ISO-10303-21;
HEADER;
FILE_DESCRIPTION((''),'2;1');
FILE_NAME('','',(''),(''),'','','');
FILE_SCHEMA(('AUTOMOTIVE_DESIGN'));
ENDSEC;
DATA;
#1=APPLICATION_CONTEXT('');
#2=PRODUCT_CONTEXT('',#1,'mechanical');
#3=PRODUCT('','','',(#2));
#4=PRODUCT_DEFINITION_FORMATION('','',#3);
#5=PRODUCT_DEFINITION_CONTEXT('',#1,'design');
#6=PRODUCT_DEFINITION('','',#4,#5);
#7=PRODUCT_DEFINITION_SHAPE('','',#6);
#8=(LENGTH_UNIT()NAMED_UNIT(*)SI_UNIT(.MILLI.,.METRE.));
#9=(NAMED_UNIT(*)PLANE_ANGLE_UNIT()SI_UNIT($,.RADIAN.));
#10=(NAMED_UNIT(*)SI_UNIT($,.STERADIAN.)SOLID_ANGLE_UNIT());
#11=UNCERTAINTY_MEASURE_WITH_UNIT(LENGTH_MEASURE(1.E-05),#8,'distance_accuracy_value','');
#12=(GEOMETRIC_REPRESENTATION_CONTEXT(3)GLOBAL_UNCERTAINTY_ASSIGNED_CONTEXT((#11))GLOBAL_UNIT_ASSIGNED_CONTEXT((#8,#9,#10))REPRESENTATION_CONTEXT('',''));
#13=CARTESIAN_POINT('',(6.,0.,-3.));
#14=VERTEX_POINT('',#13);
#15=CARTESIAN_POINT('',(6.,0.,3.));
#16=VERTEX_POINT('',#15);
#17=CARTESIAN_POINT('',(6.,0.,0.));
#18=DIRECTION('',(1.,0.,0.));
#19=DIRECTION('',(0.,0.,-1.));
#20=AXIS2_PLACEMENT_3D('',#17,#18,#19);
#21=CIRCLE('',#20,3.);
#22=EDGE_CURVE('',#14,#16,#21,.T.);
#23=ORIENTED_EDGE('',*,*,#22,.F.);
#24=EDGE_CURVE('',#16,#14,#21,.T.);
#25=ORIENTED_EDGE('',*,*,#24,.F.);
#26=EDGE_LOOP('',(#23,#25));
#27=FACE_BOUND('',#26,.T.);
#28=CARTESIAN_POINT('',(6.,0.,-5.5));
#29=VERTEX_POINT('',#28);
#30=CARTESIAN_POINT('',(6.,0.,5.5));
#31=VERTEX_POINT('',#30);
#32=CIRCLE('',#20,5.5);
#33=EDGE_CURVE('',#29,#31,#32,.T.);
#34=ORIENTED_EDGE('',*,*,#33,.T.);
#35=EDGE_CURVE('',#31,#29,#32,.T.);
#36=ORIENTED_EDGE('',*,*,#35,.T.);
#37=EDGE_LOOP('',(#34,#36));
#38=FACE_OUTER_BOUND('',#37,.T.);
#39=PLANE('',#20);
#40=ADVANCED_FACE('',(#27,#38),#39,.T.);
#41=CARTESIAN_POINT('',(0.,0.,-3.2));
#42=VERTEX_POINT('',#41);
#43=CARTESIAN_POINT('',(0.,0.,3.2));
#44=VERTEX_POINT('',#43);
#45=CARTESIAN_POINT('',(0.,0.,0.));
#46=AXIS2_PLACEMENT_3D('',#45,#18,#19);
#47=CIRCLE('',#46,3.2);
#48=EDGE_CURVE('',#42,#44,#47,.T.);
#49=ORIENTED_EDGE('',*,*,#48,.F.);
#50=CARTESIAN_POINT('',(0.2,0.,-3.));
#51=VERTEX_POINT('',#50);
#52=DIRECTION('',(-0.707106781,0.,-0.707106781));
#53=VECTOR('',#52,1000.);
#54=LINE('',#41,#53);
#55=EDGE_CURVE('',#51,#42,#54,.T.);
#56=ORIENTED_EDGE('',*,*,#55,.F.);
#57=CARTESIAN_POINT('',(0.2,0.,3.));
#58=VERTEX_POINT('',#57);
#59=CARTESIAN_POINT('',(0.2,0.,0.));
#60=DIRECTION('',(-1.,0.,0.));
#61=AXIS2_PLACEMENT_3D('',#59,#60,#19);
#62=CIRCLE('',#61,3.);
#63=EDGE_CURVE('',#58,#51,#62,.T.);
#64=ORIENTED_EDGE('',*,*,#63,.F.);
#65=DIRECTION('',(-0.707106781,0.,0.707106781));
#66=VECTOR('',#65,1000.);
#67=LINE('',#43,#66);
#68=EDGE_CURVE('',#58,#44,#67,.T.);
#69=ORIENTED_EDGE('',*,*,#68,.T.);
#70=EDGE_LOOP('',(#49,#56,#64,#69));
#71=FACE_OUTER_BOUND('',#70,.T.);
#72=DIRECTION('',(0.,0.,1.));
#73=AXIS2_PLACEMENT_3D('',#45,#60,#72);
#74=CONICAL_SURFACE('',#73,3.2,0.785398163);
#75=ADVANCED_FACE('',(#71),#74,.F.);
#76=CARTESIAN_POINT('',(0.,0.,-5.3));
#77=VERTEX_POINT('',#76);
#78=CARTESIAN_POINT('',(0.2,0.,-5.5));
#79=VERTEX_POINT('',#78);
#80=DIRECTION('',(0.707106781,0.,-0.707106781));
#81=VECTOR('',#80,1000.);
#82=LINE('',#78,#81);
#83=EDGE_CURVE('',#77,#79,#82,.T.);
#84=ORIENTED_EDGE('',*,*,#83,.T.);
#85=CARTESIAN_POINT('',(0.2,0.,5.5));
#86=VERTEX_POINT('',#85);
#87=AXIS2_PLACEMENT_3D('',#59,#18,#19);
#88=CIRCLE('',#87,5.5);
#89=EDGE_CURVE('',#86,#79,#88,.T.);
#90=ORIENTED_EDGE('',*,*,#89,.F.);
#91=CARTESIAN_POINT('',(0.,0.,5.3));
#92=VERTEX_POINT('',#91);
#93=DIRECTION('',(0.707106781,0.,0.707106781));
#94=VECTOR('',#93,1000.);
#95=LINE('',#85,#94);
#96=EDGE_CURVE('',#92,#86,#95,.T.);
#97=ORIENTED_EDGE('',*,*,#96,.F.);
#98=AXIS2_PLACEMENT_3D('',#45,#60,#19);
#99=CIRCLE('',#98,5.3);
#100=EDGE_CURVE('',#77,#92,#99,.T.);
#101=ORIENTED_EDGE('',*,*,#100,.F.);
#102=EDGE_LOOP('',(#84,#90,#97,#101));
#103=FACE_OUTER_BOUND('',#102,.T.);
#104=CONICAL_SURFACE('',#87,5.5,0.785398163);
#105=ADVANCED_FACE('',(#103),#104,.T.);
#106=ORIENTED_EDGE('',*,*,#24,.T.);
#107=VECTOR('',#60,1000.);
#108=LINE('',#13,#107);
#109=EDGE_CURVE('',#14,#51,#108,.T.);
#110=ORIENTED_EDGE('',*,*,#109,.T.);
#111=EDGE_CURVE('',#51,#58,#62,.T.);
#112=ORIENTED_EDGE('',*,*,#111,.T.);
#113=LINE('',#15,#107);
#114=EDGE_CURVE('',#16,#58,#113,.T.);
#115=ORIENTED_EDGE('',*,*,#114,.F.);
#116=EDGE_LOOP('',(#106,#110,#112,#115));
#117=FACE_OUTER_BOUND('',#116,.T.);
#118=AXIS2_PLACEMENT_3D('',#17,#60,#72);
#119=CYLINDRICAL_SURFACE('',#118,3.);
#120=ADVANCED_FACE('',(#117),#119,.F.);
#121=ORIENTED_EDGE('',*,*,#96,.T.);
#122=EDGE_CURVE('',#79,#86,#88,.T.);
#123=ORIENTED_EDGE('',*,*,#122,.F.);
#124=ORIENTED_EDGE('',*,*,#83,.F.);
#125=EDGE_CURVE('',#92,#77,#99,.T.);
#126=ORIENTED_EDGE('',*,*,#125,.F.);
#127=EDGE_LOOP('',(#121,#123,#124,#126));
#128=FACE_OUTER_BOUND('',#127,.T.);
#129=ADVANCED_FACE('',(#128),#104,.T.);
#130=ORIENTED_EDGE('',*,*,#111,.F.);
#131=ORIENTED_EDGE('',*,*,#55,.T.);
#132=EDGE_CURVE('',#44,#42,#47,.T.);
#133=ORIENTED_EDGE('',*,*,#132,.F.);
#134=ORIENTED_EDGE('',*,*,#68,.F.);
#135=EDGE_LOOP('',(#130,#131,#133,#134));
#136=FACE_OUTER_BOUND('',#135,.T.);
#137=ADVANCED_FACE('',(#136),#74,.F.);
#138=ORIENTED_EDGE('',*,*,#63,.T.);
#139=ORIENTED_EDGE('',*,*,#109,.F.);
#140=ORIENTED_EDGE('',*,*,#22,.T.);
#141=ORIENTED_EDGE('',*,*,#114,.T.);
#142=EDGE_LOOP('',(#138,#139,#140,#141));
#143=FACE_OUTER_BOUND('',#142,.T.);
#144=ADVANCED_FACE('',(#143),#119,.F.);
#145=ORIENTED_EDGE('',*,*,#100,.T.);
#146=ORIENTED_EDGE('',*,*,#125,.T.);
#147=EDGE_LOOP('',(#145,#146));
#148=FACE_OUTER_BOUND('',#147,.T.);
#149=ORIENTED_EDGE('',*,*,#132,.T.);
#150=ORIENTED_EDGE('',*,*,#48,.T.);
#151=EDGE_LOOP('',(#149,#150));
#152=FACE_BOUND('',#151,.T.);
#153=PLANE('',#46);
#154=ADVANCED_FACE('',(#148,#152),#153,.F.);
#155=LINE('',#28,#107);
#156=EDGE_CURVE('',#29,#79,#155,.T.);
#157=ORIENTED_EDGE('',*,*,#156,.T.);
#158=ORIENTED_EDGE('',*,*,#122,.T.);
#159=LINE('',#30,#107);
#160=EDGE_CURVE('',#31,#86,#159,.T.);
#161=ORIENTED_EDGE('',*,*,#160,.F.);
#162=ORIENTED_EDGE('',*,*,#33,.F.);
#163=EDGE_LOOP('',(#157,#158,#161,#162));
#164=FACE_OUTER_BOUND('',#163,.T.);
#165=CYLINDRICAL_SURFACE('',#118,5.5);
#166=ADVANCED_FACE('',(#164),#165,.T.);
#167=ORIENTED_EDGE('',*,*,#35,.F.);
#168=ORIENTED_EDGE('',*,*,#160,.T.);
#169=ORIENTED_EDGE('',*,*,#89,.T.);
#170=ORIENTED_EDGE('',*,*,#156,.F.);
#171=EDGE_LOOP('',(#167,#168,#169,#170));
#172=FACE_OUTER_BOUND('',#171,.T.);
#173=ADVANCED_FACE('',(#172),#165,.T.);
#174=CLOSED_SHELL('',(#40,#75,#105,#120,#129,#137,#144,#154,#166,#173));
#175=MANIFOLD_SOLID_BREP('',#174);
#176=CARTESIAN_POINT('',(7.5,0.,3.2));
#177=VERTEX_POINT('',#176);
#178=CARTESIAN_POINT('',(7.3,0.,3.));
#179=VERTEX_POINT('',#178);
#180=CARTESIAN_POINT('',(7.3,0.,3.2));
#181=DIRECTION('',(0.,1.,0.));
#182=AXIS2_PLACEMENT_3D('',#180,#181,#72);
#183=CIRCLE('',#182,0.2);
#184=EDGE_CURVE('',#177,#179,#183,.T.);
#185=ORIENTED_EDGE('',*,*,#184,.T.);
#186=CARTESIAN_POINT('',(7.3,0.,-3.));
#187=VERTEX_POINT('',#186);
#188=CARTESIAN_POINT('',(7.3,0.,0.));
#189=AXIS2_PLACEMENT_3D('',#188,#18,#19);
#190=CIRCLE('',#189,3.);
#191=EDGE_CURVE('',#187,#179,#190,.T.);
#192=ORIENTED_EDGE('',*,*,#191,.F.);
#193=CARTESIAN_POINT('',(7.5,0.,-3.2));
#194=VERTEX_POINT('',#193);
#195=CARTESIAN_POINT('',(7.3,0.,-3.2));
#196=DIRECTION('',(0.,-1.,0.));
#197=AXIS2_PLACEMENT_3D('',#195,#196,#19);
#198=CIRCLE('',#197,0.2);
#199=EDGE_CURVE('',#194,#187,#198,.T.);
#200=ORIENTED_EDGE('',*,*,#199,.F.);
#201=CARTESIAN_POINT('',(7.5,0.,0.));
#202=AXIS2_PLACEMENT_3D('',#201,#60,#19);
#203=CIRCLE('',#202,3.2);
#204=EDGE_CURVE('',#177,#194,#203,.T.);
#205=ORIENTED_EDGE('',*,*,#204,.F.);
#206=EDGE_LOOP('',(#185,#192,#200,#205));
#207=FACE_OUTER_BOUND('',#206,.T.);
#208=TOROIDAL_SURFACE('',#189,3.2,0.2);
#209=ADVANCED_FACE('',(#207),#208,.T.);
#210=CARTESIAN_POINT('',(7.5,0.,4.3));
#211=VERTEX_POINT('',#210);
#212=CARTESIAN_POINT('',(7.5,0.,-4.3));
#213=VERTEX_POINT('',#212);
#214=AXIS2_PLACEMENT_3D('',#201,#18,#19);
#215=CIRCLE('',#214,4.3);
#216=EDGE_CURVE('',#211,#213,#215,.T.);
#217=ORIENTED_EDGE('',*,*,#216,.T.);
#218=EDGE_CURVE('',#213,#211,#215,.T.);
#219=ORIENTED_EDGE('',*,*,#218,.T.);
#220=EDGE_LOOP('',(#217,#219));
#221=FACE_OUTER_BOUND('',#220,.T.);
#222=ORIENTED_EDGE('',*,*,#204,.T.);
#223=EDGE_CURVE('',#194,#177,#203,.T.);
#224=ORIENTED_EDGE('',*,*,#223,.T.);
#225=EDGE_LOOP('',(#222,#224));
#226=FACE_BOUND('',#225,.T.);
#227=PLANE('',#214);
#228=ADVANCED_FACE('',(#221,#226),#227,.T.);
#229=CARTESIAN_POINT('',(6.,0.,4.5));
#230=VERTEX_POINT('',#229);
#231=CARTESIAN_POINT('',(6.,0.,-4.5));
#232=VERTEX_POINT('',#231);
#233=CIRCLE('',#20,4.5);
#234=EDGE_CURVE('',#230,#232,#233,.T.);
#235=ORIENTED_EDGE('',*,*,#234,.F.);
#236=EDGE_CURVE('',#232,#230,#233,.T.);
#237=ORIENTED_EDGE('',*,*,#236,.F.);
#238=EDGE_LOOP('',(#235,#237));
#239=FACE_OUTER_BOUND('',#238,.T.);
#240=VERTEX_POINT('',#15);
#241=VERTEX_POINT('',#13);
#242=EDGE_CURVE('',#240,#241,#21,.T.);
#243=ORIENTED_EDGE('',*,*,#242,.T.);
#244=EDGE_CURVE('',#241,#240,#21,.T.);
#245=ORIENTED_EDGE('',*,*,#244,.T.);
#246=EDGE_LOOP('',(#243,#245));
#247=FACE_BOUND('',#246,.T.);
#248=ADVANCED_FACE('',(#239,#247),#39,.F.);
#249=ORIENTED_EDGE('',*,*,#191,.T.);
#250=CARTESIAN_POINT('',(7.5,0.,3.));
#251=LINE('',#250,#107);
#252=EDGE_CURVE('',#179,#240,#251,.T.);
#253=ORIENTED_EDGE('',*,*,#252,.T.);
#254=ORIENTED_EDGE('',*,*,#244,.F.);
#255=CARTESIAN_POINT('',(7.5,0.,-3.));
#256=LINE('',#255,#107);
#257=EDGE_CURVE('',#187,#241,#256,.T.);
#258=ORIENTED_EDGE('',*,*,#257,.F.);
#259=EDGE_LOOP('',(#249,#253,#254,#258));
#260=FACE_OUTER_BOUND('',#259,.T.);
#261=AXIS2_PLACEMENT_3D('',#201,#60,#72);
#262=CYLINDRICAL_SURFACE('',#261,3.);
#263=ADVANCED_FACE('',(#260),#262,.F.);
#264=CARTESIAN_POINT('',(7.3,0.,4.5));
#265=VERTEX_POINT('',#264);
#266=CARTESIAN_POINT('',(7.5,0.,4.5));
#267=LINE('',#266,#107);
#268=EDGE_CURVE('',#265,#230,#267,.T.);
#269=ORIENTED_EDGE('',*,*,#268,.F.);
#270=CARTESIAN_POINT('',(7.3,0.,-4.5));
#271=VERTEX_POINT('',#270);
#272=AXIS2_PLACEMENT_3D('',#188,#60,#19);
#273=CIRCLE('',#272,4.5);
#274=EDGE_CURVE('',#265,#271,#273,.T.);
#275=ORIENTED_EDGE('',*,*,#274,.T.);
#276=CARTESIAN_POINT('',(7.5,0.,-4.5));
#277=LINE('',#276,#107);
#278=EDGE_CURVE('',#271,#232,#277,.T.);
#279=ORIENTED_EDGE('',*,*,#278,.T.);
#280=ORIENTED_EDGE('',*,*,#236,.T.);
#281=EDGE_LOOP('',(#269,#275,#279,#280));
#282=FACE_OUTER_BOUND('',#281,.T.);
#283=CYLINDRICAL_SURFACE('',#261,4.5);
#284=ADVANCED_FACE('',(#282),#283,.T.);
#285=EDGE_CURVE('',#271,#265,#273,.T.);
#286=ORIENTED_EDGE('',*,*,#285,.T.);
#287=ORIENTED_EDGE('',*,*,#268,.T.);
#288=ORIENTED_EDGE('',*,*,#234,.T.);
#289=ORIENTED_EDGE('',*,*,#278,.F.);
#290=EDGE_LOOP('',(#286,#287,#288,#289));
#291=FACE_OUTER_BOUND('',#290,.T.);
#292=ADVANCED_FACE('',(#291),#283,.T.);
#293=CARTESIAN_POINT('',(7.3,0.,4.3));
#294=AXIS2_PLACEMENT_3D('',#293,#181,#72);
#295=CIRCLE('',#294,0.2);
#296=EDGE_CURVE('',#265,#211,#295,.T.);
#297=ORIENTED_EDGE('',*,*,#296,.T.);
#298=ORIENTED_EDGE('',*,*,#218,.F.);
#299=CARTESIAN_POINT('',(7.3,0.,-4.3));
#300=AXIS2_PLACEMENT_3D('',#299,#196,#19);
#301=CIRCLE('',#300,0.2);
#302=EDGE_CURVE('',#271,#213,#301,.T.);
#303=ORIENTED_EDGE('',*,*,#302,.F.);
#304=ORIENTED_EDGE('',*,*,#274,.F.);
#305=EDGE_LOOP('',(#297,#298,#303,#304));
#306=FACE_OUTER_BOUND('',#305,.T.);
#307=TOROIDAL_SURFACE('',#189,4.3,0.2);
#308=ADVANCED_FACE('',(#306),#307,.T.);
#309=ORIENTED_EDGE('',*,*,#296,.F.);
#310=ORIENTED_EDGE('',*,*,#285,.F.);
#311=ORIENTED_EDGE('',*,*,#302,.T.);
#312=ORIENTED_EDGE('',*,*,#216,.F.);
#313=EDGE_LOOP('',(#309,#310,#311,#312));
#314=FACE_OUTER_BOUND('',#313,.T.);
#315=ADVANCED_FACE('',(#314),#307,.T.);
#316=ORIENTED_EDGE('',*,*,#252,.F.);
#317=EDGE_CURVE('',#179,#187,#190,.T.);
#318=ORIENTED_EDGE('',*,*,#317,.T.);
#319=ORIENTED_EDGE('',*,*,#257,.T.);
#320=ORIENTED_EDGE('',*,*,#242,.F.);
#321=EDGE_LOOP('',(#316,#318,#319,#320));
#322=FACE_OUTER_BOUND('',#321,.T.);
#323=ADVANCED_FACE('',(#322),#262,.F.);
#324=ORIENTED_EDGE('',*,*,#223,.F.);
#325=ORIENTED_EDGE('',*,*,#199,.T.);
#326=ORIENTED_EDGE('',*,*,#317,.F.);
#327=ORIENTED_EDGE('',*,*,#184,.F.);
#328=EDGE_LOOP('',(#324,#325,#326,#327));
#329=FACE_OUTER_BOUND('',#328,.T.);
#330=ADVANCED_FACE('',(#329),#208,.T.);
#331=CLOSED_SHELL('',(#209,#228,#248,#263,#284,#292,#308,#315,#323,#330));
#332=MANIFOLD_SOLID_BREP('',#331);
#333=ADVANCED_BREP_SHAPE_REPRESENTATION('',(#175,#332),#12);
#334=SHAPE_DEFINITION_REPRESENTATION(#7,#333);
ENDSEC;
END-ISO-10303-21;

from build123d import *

# Parameters (mm, degrees)
SKETCH_1_R      = 5.5
SKETCH_1_R_2    = 3
EXTRUDE_1_DEPTH = 6
SKETCH_3_R      = 4.5
SKETCH_3_R_2    = 3
EXTRUDE_2_DEPTH = 1.5
FILLET_1_R      = 0.2
CHAMFER_1_SIZE  = 0.2


with BuildPart() as part:
    # 草图1 → 凸台-拉伸1 (new body)
    with BuildSketch(Plane(origin=(0, 0, 0), x_dir=(0, 0, -1), z_dir=(1, 0, 0))):
        Circle(SKETCH_1_R)
        Circle(SKETCH_1_R_2, mode=Mode.SUBTRACT)
    extrude(amount=EXTRUDE_1_DEPTH)

    # 倒角1
    chamfer_1_edges = [part.edges().sort_by_distance(p)[0] for p in [
        (0, 0, 5.5),
        (0, 0, 3),
    ]]
    chamfer(chamfer_1_edges, length=CHAMFER_1_SIZE)


with BuildPart() as body_2:
    # 草图3 → 凸台-拉伸2 (new body)
    with BuildSketch(Plane(origin=(6, 0, 0), x_dir=(0, 0, -1), z_dir=(1, 0, 0))):
        Circle(SKETCH_3_R)
        Circle(SKETCH_3_R_2, mode=Mode.SUBTRACT)
    extrude(amount=EXTRUDE_2_DEPTH)

    # 圆角1
    fillet_1_edges = [body_2.edges().sort_by_distance(p)[0] for p in [
        (7.5, 0, 4.5),
        (7.5, 0, 3),
    ]]
    fillet(fillet_1_edges, radius=FILLET_1_R)


solid = Compound([part.part, body_2.part])
